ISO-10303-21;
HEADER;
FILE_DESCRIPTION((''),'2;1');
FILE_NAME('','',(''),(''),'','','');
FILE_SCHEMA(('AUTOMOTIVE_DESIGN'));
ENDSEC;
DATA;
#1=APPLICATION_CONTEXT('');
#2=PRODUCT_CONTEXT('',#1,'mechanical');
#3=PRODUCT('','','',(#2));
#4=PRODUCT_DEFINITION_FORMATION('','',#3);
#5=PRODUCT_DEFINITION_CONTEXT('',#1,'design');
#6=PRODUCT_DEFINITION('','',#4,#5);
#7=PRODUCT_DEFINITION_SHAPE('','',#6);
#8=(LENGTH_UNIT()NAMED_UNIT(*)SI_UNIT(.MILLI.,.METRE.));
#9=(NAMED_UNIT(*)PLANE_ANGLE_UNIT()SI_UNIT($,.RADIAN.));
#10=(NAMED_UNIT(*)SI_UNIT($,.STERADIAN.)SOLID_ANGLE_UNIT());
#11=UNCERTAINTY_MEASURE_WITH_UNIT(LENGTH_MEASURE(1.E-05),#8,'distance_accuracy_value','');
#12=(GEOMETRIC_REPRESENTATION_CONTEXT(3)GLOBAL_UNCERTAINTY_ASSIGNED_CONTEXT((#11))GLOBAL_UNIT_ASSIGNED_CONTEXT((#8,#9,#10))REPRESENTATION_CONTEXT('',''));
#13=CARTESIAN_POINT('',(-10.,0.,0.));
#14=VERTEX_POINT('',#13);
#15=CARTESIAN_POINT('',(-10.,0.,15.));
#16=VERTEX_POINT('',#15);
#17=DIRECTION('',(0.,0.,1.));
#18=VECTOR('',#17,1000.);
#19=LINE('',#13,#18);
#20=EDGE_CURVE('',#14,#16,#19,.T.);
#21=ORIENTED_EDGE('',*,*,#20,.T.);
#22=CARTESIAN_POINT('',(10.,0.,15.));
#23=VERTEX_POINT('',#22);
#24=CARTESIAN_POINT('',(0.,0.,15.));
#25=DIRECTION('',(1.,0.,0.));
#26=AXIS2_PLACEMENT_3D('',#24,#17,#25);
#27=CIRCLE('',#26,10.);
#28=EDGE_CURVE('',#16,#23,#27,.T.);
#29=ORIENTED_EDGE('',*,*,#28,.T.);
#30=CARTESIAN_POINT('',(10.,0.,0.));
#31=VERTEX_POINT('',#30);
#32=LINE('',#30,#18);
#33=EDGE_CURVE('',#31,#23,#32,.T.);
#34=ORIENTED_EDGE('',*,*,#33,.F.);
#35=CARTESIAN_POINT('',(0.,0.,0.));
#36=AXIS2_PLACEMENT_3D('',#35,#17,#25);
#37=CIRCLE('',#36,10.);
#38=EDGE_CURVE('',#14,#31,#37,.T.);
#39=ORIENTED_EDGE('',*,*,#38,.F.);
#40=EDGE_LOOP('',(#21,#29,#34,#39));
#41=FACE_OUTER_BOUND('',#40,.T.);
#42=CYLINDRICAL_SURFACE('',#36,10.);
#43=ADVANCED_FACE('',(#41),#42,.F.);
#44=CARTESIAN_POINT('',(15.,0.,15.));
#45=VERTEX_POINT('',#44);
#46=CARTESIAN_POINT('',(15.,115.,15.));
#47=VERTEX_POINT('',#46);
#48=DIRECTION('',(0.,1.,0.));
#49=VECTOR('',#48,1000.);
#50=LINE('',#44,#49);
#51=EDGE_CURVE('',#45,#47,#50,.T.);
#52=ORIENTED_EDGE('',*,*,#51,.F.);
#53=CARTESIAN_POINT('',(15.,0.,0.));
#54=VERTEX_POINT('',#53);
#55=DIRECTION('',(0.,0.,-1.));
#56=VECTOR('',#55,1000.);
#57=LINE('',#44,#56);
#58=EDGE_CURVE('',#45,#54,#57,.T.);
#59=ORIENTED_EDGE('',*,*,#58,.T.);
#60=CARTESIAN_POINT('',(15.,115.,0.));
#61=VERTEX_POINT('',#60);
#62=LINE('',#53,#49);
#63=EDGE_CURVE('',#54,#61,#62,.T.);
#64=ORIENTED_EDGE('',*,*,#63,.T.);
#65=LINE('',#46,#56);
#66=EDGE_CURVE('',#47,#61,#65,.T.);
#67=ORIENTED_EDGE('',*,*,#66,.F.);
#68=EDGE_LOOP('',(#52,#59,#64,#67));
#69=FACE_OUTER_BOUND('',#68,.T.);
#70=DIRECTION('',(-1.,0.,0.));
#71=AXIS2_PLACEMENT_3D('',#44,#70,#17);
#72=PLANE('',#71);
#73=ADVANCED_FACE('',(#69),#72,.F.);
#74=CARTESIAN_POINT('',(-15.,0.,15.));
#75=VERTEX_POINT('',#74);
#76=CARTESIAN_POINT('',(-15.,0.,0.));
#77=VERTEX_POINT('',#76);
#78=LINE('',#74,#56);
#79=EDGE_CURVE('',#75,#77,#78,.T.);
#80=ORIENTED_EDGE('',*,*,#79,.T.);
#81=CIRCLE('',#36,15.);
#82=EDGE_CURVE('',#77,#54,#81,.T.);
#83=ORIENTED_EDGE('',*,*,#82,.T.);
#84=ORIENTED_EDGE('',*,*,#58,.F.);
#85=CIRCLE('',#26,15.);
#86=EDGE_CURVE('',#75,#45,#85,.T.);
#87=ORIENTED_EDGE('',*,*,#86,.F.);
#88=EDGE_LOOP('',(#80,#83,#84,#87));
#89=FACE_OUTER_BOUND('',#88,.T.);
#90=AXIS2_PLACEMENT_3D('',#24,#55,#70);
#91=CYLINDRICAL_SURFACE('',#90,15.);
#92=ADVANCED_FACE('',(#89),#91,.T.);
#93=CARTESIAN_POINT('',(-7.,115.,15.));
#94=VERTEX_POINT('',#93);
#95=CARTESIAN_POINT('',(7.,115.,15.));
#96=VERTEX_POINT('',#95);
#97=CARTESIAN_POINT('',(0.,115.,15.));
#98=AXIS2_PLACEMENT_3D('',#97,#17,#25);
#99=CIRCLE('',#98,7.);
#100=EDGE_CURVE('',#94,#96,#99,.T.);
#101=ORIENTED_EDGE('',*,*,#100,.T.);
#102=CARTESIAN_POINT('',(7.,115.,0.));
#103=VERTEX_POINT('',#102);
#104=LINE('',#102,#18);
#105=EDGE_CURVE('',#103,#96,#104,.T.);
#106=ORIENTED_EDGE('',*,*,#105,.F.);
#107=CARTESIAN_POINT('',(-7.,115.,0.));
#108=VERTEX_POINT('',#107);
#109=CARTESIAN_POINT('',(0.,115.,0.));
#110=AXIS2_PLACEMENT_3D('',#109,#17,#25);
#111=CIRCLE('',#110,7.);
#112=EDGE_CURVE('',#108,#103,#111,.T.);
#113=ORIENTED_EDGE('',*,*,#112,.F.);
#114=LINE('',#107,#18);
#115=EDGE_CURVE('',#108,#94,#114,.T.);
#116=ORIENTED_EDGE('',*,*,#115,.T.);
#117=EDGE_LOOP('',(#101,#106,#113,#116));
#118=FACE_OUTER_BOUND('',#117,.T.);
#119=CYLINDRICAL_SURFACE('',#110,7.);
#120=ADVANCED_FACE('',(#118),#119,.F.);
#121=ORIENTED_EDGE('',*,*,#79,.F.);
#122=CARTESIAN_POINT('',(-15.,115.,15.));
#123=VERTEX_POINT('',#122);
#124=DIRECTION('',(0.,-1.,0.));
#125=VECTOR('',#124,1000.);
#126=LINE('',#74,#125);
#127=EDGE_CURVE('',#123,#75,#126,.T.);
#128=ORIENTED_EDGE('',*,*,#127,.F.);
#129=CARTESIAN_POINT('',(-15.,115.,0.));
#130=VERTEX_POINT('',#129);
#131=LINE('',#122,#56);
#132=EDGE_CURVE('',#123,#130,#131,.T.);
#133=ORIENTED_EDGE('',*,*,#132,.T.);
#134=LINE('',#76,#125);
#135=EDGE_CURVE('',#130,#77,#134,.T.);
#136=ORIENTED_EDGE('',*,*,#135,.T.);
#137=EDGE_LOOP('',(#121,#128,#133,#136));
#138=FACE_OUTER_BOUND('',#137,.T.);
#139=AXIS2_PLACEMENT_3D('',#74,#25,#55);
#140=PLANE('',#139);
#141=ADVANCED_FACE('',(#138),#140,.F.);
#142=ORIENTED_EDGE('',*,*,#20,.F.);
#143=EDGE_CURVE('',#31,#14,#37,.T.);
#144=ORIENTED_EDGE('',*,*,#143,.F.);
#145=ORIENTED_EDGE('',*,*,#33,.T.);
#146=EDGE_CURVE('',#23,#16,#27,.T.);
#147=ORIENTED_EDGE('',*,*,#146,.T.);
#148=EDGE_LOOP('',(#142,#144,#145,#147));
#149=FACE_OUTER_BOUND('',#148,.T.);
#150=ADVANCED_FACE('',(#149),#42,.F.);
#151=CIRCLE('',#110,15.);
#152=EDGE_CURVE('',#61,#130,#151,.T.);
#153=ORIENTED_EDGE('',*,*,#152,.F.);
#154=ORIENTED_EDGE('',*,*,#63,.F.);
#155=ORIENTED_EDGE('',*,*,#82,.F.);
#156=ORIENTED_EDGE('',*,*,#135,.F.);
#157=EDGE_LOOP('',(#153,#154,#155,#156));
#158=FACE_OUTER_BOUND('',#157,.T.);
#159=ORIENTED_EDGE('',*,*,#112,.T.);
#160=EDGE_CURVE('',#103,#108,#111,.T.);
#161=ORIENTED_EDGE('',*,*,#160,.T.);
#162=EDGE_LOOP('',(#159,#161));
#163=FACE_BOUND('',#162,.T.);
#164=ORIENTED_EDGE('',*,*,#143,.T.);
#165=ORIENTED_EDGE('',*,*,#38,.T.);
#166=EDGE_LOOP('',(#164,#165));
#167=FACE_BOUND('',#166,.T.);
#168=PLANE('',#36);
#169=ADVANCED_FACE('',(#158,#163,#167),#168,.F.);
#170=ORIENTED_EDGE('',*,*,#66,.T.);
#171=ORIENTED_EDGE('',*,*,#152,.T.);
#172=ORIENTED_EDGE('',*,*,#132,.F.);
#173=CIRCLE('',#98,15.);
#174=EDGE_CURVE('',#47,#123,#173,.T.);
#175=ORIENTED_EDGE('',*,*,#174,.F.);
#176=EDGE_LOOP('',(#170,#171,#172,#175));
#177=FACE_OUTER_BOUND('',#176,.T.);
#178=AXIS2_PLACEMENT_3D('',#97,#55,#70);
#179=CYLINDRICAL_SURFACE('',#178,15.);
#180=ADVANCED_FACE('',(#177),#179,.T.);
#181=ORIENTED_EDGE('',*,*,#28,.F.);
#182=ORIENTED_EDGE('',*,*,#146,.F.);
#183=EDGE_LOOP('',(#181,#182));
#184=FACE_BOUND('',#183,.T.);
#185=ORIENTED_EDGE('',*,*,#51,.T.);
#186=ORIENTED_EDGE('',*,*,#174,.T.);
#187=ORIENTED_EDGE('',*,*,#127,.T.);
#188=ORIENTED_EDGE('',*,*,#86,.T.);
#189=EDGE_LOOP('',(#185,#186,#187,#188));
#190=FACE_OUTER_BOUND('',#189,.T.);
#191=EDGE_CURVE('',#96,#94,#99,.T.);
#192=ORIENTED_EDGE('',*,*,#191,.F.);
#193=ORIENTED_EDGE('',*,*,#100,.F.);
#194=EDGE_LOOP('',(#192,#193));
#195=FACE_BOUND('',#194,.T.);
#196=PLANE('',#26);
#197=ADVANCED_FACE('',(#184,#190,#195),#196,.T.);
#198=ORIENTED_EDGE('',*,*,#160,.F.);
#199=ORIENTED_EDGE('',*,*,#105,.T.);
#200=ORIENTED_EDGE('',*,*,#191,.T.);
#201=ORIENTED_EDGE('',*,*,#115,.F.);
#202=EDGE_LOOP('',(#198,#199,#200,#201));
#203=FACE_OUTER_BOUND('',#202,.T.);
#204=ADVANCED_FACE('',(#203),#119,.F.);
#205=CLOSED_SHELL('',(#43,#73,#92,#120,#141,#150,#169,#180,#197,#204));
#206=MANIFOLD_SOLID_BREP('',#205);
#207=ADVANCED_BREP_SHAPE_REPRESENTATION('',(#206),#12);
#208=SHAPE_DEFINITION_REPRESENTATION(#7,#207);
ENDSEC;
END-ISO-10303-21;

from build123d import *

# Parameters (mm, degrees)
EXTRUDE_1_DEPTH     = 15
SKETCH_2_R          = 7
SKETCH_2_R_2        = 10
CUT_EXTRUDE_1_DEPTH = 132.719398723


with BuildPart() as part:
    # 草图1 → 凸台-拉伸1 (new body)
    with BuildSketch(Plane.XY):
        with BuildLine():
            Line((-15, 0), (-15, 115))
            ThreePointArc((-15, 115), (0, 130), (15, 115))
            Line((15, 115), (15, 0))
            ThreePointArc((15, 0), (0, -15), (-15, 0))
        make_face()
    extrude(amount=EXTRUDE_1_DEPTH)

    # 草图2 → 切除-拉伸1 (cut, through all)
    with BuildSketch(Plane.XY.offset(15)):
        with Locations((0, 115)):
            Circle(SKETCH_2_R)
        Circle(SKETCH_2_R_2)
    extrude(amount=-CUT_EXTRUDE_1_DEPTH, mode=Mode.SUBTRACT)


solid = part.part
